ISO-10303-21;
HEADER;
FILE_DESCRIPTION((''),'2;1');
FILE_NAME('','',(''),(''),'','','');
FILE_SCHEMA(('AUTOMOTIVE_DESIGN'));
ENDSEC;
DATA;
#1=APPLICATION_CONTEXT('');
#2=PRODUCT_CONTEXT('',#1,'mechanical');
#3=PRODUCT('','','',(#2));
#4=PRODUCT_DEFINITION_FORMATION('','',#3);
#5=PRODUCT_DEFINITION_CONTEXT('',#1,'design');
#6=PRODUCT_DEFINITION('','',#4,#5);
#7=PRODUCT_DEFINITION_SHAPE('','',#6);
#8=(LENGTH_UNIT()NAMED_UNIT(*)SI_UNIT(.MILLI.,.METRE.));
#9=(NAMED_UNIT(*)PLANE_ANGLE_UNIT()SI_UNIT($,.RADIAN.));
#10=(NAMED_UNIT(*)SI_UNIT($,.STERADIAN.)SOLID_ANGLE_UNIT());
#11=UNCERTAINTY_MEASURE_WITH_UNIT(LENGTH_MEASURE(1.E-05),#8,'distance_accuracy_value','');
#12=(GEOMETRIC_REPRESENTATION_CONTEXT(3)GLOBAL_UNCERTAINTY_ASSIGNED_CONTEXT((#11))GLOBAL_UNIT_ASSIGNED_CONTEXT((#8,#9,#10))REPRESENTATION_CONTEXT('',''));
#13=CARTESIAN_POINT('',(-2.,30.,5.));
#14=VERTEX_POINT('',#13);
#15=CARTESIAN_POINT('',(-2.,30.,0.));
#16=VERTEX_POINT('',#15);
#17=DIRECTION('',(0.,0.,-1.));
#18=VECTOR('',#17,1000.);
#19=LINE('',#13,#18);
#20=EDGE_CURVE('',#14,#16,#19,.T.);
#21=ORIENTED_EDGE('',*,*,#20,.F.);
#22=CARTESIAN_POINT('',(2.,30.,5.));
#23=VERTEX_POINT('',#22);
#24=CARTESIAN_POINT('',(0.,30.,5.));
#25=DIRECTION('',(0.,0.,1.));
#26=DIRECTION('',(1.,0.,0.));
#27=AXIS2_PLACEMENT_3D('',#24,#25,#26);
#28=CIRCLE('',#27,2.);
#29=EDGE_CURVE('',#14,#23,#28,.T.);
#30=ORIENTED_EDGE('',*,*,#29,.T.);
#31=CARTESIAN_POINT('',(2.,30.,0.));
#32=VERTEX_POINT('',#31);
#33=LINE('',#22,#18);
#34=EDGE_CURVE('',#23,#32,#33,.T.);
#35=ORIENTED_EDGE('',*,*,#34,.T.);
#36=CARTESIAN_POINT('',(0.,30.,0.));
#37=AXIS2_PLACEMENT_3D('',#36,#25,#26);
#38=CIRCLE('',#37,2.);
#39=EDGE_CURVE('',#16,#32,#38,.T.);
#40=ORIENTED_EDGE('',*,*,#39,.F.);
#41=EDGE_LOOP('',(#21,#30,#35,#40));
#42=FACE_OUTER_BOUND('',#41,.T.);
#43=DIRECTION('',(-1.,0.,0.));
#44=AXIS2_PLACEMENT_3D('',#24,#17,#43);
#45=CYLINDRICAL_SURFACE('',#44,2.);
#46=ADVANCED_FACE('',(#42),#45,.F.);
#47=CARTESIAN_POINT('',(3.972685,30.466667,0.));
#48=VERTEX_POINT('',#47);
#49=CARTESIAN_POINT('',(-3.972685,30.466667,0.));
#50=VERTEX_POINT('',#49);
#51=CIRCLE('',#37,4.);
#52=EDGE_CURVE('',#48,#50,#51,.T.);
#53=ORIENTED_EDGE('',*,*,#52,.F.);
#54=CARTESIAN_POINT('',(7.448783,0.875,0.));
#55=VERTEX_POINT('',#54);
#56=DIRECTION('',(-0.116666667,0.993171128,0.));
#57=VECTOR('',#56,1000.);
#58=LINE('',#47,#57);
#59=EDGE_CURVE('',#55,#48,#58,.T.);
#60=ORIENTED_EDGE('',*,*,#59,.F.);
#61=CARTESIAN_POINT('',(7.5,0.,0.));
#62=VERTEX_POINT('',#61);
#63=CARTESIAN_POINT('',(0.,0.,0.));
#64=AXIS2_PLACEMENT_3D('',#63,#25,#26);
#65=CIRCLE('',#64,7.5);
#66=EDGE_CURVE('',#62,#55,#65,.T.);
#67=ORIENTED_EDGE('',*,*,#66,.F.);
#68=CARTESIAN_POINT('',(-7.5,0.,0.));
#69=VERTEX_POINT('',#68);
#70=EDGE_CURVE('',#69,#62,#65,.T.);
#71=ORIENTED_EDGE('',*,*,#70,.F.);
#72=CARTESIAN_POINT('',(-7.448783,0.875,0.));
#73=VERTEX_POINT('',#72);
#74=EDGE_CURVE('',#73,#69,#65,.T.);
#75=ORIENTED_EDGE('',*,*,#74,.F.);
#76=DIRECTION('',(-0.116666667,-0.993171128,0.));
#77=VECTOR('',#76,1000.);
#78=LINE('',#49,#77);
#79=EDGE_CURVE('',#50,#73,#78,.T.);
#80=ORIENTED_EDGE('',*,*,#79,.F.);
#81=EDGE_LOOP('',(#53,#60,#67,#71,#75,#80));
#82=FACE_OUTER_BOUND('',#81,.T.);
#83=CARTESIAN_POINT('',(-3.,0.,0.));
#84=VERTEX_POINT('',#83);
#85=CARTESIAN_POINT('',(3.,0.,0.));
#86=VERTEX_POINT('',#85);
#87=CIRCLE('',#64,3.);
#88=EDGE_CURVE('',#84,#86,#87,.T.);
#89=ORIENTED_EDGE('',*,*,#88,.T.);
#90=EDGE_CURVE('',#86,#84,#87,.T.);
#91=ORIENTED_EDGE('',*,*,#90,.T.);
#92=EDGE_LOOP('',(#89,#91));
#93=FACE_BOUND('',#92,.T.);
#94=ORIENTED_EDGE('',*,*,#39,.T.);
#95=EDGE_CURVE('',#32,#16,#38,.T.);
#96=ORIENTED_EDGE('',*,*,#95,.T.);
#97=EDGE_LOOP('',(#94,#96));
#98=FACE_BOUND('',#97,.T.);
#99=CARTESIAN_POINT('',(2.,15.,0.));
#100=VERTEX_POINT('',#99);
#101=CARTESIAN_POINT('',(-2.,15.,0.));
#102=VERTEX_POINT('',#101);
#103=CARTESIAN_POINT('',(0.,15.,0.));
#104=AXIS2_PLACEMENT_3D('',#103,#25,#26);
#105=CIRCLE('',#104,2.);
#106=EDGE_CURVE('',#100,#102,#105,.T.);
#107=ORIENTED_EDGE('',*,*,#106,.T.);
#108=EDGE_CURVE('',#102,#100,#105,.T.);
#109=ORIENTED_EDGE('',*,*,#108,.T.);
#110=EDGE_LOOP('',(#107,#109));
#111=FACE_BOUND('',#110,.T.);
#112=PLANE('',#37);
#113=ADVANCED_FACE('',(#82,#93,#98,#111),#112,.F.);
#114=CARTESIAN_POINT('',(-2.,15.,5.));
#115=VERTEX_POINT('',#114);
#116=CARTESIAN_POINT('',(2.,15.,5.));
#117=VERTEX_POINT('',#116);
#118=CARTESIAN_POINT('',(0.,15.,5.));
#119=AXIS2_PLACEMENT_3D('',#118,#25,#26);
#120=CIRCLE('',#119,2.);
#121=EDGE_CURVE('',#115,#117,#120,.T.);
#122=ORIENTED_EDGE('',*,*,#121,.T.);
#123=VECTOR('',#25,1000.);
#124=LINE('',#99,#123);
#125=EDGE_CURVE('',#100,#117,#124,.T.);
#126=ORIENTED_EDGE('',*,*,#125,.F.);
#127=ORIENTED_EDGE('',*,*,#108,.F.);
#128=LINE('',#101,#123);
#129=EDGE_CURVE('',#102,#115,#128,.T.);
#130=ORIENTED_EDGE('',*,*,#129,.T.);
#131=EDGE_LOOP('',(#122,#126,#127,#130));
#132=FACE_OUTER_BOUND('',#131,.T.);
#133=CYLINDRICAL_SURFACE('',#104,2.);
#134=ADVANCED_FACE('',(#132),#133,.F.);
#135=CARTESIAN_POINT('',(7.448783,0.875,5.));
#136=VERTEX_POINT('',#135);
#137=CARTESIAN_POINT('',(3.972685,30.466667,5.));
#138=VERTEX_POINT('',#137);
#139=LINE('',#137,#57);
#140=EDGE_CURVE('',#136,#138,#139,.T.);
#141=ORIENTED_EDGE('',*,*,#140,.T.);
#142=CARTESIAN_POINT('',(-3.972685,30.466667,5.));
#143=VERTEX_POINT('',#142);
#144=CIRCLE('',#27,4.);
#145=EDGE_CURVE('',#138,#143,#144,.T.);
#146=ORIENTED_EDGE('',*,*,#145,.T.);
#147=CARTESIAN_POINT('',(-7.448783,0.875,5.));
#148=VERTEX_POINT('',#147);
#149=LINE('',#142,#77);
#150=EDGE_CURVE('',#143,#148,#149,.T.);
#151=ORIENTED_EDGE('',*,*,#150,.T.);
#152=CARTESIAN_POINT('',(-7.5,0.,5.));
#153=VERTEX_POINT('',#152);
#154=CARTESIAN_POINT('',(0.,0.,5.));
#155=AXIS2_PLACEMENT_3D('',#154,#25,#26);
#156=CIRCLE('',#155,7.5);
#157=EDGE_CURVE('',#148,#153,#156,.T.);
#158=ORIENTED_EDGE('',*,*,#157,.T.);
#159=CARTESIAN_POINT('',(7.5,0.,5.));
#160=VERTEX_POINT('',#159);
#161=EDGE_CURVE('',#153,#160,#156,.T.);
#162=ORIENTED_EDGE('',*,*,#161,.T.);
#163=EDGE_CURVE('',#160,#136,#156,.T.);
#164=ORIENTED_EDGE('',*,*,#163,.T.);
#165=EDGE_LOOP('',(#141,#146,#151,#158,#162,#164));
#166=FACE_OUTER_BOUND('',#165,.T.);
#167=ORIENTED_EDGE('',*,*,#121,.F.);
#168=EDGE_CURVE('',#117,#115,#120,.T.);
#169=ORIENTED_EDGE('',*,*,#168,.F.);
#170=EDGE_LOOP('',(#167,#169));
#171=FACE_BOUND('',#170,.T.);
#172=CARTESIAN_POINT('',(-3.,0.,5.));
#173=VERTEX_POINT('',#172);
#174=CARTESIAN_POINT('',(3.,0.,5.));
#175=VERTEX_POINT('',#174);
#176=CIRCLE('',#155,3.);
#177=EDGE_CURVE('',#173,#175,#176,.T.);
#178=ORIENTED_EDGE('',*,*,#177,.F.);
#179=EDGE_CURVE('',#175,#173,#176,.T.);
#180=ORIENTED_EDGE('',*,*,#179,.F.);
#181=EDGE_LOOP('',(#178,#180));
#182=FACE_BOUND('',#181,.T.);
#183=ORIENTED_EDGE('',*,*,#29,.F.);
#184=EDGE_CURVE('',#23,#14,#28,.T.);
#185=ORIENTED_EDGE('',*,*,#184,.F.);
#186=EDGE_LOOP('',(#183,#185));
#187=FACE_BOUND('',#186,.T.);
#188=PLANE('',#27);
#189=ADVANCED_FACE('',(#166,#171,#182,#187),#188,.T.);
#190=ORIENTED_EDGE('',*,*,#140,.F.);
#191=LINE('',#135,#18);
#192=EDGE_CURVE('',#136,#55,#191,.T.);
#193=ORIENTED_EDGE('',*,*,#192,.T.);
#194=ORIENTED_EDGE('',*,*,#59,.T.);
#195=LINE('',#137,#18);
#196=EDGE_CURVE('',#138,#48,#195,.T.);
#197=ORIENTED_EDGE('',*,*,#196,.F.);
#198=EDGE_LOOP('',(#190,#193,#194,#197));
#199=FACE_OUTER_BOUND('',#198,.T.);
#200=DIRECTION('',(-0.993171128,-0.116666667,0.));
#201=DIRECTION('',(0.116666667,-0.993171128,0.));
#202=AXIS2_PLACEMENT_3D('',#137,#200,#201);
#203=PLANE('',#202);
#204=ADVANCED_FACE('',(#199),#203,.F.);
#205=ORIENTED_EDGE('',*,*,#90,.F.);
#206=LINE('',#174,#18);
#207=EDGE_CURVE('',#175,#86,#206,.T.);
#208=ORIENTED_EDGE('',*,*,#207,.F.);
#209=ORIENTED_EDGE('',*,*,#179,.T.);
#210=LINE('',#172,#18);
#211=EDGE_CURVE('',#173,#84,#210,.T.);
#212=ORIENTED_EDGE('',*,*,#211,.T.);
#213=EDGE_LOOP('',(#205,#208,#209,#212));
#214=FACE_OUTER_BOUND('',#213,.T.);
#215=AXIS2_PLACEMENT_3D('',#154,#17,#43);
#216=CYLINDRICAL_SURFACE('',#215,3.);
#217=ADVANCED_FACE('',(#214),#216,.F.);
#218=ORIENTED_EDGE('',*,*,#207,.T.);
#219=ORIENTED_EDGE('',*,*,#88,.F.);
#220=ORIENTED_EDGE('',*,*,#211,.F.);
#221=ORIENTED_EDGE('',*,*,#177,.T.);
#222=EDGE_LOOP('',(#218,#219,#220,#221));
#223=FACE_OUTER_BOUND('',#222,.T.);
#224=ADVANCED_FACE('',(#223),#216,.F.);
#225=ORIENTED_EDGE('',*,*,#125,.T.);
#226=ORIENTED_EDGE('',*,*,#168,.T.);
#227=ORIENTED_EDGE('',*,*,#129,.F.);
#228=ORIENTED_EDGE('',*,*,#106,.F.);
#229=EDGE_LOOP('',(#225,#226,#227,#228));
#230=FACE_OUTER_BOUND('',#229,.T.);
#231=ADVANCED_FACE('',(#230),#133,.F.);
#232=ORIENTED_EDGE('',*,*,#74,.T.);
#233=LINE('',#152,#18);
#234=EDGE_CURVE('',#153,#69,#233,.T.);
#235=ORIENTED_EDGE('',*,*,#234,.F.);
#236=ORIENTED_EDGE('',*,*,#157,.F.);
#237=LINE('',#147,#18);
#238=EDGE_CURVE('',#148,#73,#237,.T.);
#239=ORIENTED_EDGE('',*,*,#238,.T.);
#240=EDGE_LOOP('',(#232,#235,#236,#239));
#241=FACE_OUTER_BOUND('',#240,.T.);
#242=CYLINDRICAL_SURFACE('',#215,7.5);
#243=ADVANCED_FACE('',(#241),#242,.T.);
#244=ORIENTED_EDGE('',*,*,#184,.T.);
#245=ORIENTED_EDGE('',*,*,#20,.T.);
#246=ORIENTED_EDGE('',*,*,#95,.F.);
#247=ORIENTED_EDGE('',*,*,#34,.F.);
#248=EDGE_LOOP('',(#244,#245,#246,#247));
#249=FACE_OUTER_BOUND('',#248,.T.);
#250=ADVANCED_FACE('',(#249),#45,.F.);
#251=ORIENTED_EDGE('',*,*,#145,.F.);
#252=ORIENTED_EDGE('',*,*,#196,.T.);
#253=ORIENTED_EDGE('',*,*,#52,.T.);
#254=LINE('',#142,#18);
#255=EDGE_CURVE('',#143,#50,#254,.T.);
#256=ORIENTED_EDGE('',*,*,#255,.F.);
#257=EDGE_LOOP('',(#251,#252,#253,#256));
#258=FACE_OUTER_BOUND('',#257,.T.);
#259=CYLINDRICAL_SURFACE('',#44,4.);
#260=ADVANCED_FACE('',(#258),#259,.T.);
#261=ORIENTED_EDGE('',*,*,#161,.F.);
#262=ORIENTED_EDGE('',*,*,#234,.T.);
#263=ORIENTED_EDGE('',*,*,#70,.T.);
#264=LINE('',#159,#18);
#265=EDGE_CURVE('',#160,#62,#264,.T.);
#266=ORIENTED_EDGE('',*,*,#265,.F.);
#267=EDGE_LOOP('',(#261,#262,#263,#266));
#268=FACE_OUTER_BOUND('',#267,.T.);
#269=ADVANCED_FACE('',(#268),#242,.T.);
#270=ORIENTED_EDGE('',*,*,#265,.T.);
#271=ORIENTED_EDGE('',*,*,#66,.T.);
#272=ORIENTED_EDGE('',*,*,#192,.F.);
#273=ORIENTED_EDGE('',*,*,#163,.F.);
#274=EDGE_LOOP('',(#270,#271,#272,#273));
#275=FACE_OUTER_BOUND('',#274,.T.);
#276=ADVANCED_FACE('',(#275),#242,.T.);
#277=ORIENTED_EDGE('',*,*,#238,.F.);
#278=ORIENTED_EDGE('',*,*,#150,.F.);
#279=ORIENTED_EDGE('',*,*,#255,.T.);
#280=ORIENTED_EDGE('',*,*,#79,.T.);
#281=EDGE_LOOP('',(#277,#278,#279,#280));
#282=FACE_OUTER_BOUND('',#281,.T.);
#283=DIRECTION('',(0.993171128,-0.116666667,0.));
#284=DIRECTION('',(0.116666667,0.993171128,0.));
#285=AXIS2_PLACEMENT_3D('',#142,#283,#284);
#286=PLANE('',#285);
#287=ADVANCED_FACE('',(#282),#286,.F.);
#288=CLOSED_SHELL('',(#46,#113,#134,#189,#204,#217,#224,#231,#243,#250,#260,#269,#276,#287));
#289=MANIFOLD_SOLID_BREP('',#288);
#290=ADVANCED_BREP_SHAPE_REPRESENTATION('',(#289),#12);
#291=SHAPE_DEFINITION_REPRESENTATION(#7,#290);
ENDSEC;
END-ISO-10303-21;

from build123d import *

# Parameters (mm, degrees)
SKETCH1_R           = 2
SKETCH1_R_2         = 3
BOSS_EXTRUDE1_DEPTH = 5
SKETCH2_R           = 2
CUT_EXTRUDE1_DEPTH  = 36.174564674


with BuildPart() as part:
    # Sketch1 → Boss-Extrude1 (new body)
    with BuildSketch(Plane.XY):
        with BuildLine():
            Line((-3.972684511, 30.466666667), (-7.448783458, 0.875))
            ThreePointArc((-7.448783458, 0.875), (0, -7.5), (7.448783458, 0.875))
            Line((7.448783458, 0.875), (3.972684511, 30.466666667))
            ThreePointArc((3.972684511, 30.466666667), (0, 34), (-3.972684511, 30.466666667))
        make_face()
        with Locations((0, 30)):
            Circle(SKETCH1_R, mode=Mode.SUBTRACT)
        Circle(SKETCH1_R_2, mode=Mode.SUBTRACT)
    extrude(amount=BOSS_EXTRUDE1_DEPTH)

    # Sketch2 → Cut-Extrude1 (cut, through all)
    with BuildSketch(Plane.XY.offset(5)):
        with Locations((0, 15)):
            Circle(SKETCH2_R)
    extrude(amount=-CUT_EXTRUDE1_DEPTH, mode=Mode.SUBTRACT)


solid = part.part
